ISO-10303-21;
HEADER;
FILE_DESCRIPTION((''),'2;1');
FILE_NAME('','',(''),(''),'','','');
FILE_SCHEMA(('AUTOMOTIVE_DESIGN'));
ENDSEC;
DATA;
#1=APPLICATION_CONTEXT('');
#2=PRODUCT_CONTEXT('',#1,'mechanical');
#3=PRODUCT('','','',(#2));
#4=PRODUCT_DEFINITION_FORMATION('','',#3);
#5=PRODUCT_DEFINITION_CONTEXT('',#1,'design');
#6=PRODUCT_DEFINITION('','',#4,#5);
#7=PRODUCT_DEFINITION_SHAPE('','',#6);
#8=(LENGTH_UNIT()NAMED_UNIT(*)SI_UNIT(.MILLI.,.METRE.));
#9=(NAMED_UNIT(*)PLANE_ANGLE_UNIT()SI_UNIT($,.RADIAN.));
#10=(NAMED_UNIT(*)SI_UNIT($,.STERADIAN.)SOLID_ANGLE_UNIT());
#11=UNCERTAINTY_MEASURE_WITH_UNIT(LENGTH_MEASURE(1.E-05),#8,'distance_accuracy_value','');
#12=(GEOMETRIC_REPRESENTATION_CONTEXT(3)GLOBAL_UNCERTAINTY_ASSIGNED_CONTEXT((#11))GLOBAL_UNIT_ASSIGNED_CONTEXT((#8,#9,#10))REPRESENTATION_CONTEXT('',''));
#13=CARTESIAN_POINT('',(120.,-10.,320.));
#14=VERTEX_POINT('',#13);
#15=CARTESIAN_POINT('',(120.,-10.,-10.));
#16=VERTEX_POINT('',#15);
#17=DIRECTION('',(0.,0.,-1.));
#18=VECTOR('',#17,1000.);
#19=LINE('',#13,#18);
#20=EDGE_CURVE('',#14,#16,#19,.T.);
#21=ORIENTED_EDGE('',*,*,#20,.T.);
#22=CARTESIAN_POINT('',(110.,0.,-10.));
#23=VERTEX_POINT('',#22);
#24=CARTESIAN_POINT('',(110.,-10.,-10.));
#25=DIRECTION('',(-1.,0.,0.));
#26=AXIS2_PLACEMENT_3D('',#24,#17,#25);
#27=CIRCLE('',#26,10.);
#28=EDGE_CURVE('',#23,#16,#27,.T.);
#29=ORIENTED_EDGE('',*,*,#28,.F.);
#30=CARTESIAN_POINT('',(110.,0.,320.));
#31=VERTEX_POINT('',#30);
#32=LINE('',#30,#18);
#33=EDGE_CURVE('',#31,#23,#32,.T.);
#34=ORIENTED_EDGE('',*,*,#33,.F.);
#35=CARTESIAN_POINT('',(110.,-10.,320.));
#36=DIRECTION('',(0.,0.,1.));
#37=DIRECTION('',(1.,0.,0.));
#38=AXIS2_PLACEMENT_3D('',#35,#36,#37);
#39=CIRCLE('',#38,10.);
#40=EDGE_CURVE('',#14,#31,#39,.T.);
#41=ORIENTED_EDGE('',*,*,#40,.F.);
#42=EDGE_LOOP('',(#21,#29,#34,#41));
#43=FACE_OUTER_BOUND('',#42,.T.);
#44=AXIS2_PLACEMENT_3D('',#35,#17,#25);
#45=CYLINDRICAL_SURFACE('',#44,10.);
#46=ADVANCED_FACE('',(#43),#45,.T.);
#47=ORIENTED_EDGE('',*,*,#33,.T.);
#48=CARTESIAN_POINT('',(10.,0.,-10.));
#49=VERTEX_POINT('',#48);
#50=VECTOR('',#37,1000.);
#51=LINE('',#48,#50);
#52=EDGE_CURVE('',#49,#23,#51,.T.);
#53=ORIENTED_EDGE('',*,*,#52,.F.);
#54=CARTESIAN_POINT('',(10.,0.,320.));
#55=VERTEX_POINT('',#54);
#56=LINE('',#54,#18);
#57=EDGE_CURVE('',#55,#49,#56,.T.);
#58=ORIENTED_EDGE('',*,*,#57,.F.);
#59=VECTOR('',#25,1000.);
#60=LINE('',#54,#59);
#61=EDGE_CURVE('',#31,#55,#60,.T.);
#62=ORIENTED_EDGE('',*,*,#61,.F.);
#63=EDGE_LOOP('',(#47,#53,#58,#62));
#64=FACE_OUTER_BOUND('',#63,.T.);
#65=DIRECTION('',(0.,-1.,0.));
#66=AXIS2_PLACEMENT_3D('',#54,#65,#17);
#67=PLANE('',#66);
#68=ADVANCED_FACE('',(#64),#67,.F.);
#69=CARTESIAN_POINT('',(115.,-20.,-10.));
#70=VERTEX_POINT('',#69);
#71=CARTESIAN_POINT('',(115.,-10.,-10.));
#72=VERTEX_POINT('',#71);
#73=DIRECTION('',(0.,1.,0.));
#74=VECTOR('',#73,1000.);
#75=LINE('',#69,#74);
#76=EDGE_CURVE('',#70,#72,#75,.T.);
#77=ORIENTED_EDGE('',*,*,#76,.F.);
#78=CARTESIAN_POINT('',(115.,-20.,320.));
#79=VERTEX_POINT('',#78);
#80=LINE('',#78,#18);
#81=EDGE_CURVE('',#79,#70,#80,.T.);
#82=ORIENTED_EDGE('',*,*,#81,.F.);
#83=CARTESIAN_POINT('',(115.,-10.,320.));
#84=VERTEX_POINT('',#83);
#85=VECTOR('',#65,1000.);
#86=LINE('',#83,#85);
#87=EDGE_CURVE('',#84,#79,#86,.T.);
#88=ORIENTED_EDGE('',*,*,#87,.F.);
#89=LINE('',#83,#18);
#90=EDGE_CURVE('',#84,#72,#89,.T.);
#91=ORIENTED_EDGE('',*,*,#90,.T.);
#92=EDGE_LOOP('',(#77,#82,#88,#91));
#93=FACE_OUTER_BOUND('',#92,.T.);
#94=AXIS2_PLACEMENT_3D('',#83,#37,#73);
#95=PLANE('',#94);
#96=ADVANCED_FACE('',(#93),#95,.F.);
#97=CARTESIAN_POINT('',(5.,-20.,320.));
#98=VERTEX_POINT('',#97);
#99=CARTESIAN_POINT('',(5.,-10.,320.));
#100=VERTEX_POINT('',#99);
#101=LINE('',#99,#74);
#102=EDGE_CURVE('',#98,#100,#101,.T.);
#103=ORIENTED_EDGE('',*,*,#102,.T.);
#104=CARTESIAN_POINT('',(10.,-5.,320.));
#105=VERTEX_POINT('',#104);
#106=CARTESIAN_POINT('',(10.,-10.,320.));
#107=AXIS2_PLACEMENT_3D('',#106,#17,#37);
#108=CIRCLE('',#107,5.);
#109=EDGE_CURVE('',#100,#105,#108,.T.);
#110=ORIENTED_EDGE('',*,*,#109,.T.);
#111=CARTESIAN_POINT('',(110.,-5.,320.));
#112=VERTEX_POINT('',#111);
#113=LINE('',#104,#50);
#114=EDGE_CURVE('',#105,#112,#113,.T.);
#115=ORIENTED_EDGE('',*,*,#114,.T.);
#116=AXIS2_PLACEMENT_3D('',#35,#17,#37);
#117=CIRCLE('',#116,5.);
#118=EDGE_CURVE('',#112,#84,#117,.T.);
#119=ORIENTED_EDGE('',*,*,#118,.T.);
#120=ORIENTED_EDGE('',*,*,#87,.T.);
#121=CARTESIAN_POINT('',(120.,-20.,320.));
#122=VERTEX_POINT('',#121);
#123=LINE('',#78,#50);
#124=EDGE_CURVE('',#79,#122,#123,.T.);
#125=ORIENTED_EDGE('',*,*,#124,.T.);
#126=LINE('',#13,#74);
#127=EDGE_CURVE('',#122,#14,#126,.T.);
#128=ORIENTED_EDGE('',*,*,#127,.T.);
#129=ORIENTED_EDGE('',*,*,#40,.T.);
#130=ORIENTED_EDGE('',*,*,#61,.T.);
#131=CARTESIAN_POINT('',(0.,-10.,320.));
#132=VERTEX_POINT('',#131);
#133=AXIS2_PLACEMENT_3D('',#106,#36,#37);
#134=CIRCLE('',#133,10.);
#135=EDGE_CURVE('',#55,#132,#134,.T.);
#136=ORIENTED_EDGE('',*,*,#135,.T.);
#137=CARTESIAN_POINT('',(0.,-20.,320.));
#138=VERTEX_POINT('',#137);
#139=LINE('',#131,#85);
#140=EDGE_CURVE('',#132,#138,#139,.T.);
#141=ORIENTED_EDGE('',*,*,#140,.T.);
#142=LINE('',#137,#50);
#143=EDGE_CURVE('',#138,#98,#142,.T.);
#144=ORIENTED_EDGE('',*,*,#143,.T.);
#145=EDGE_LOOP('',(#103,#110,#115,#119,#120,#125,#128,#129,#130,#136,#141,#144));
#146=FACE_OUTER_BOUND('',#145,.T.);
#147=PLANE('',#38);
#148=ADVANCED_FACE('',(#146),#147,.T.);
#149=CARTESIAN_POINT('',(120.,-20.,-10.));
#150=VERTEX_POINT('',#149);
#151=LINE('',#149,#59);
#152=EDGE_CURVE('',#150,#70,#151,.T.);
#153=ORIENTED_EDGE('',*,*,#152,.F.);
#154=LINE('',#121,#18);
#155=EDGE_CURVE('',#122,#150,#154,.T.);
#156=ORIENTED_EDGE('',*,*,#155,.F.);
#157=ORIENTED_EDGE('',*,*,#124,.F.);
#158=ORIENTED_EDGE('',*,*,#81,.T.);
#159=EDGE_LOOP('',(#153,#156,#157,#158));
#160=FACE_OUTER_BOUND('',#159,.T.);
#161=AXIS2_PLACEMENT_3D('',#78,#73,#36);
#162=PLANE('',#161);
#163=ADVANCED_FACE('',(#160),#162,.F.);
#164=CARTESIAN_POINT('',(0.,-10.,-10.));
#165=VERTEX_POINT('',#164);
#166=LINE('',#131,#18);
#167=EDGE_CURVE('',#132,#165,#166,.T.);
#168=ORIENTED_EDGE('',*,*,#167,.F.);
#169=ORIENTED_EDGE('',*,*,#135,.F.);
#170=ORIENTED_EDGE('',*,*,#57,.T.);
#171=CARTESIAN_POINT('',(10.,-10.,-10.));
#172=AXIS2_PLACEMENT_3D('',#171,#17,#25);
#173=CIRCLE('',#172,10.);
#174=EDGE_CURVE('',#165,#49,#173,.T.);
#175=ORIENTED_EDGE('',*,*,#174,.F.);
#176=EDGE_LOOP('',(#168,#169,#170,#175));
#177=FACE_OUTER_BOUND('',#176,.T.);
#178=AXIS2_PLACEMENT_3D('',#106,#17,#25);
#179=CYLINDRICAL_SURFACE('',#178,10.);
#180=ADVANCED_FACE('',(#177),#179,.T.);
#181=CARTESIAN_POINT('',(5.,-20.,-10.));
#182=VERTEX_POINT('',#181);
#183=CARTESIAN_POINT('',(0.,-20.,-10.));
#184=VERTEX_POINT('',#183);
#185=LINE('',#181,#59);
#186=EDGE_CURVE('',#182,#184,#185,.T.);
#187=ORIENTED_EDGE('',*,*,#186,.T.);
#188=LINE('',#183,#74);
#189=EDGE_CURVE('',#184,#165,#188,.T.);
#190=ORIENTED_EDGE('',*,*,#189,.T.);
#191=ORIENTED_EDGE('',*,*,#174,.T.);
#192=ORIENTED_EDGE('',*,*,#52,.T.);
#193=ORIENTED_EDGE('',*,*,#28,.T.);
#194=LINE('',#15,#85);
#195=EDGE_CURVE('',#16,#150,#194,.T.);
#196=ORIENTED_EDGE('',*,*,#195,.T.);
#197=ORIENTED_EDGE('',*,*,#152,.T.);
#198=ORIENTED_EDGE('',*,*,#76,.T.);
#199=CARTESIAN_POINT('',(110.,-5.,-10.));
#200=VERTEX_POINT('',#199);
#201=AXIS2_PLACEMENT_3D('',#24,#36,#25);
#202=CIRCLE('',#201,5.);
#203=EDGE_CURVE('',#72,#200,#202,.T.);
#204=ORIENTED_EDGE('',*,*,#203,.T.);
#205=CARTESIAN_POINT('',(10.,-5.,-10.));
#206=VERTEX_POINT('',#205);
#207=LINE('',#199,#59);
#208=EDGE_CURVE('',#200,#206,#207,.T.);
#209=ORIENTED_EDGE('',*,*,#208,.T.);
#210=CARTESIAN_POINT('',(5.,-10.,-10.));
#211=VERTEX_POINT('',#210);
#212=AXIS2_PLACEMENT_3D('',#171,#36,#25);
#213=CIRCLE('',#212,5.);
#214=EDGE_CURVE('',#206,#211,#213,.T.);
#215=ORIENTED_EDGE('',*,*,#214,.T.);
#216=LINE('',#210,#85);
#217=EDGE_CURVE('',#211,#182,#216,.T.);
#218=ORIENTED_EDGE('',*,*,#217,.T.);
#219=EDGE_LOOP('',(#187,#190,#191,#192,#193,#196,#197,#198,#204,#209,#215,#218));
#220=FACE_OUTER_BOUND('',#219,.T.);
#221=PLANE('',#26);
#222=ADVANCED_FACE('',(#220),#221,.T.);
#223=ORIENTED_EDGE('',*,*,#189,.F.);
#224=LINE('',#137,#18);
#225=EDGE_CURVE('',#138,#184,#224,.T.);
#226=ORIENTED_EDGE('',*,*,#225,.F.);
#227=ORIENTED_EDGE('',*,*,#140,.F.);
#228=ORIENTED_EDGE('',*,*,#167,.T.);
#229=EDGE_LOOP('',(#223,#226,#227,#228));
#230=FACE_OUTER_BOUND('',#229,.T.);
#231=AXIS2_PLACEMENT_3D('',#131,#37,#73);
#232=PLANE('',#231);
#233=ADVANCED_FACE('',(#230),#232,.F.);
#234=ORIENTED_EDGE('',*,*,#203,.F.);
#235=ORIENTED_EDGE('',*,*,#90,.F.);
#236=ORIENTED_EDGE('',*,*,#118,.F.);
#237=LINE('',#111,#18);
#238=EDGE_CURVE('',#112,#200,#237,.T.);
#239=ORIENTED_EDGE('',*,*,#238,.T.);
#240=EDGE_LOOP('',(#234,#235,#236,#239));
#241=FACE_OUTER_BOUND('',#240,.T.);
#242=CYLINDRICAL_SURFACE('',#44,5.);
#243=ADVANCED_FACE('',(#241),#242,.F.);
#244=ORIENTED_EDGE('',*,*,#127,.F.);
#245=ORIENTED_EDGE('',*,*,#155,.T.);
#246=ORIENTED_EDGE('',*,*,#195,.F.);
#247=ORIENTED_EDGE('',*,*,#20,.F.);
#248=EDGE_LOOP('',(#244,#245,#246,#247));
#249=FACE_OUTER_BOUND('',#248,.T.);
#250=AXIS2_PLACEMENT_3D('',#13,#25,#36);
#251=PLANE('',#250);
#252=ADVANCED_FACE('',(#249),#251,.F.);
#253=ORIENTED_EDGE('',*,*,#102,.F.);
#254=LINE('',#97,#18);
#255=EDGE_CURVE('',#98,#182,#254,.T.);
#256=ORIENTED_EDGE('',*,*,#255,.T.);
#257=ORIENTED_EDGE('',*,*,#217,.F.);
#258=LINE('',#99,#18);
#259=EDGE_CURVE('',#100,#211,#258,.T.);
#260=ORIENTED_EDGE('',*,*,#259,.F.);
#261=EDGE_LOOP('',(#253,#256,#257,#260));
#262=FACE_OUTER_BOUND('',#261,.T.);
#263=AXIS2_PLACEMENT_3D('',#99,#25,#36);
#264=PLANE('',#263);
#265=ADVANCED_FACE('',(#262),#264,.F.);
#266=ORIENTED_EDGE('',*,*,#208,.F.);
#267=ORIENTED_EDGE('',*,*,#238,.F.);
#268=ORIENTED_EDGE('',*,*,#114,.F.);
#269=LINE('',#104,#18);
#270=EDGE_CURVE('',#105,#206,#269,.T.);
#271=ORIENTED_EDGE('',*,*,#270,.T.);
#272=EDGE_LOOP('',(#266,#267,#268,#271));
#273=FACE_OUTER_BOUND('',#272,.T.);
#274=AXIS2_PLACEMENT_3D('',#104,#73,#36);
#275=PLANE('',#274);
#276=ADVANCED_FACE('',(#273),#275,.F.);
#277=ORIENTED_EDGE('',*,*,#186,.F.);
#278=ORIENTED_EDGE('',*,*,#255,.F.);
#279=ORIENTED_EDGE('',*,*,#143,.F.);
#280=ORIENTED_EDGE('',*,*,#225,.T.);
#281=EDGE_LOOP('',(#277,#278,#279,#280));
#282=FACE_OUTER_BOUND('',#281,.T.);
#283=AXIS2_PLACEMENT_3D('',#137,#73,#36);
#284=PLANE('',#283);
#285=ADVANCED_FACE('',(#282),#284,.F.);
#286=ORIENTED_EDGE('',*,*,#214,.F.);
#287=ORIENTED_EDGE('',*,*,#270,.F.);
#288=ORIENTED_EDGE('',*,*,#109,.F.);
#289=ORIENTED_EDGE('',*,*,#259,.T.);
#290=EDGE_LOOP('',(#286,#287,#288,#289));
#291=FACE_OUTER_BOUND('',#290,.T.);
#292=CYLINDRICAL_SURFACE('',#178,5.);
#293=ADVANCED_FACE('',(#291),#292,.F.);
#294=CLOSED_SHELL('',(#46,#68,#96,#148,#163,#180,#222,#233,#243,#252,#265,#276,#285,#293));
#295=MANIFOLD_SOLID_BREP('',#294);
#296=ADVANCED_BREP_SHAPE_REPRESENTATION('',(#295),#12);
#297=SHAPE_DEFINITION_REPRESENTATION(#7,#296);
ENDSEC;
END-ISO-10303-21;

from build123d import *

# Parameters (mm, degrees)
EXTRUDE_1_DEPTH = 320
EXTRUDE_START   = 10
EXTRUDE_2_DEPTH = 10


with BuildPart() as part:
    # 草图1 → 凸台-拉伸1 (new body)
    with BuildSketch(Plane.XY):
        with BuildLine():
            Line((10, 0), (110, 0))
            ThreePointArc((110, 0), (117.071067812, -2.928932188), (120, -10))
            Line((120, -10), (120, -20))
            Line((120, -20), (115, -20))
            Line((115, -20), (115, -10))
            ThreePointArc((115, -10), (113.535533906, -6.464466094), (110, -5))
            Line((110, -5), (10, -5))
            ThreePointArc((10, -5), (6.464466094, -6.464466094), (5, -10))
            Line((5, -10), (5, -20))
            Line((5, -20), (0, -20))
            Line((0, -20), (0, -10))
            ThreePointArc((0, -10), (2.928932188, -2.928932188), (10, 0))
        make_face()
    extrude(amount=EXTRUDE_1_DEPTH)

    # 草图2 → 凸台-拉伸2 (add)
    with BuildSketch(Plane(origin=(0, 0, 0), x_dir=(-1, 0, 0), z_dir=(0, 0, -1)).offset(EXTRUDE_START)):
        with BuildLine():
            Line((-120, -20), (-115, -20))
            Line((-115, -20), (-115, -10))
            ThreePointArc((-115, -10), (-113.535533906, -6.464466094), (-110, -5))
            Line((-110, -5), (-10, -5))
            ThreePointArc((-10, -5), (-6.464466094, -6.464466094), (-5, -10))
            Line((-5, -10), (-5, -20))
            Line((-5, -20), (0, -20))
            Line((0, -20), (0, -10))
            ThreePointArc((0, -10), (-2.928932188, -2.928932188), (-10, 0))
            Line((-10, 0), (-110, 0))
            ThreePointArc((-110, 0), (-117.071067812, -2.928932188), (-120, -10))
            Line((-120, -10), (-120, -20))
        make_face()
    extrude(amount=-EXTRUDE_2_DEPTH)


solid = part.part
